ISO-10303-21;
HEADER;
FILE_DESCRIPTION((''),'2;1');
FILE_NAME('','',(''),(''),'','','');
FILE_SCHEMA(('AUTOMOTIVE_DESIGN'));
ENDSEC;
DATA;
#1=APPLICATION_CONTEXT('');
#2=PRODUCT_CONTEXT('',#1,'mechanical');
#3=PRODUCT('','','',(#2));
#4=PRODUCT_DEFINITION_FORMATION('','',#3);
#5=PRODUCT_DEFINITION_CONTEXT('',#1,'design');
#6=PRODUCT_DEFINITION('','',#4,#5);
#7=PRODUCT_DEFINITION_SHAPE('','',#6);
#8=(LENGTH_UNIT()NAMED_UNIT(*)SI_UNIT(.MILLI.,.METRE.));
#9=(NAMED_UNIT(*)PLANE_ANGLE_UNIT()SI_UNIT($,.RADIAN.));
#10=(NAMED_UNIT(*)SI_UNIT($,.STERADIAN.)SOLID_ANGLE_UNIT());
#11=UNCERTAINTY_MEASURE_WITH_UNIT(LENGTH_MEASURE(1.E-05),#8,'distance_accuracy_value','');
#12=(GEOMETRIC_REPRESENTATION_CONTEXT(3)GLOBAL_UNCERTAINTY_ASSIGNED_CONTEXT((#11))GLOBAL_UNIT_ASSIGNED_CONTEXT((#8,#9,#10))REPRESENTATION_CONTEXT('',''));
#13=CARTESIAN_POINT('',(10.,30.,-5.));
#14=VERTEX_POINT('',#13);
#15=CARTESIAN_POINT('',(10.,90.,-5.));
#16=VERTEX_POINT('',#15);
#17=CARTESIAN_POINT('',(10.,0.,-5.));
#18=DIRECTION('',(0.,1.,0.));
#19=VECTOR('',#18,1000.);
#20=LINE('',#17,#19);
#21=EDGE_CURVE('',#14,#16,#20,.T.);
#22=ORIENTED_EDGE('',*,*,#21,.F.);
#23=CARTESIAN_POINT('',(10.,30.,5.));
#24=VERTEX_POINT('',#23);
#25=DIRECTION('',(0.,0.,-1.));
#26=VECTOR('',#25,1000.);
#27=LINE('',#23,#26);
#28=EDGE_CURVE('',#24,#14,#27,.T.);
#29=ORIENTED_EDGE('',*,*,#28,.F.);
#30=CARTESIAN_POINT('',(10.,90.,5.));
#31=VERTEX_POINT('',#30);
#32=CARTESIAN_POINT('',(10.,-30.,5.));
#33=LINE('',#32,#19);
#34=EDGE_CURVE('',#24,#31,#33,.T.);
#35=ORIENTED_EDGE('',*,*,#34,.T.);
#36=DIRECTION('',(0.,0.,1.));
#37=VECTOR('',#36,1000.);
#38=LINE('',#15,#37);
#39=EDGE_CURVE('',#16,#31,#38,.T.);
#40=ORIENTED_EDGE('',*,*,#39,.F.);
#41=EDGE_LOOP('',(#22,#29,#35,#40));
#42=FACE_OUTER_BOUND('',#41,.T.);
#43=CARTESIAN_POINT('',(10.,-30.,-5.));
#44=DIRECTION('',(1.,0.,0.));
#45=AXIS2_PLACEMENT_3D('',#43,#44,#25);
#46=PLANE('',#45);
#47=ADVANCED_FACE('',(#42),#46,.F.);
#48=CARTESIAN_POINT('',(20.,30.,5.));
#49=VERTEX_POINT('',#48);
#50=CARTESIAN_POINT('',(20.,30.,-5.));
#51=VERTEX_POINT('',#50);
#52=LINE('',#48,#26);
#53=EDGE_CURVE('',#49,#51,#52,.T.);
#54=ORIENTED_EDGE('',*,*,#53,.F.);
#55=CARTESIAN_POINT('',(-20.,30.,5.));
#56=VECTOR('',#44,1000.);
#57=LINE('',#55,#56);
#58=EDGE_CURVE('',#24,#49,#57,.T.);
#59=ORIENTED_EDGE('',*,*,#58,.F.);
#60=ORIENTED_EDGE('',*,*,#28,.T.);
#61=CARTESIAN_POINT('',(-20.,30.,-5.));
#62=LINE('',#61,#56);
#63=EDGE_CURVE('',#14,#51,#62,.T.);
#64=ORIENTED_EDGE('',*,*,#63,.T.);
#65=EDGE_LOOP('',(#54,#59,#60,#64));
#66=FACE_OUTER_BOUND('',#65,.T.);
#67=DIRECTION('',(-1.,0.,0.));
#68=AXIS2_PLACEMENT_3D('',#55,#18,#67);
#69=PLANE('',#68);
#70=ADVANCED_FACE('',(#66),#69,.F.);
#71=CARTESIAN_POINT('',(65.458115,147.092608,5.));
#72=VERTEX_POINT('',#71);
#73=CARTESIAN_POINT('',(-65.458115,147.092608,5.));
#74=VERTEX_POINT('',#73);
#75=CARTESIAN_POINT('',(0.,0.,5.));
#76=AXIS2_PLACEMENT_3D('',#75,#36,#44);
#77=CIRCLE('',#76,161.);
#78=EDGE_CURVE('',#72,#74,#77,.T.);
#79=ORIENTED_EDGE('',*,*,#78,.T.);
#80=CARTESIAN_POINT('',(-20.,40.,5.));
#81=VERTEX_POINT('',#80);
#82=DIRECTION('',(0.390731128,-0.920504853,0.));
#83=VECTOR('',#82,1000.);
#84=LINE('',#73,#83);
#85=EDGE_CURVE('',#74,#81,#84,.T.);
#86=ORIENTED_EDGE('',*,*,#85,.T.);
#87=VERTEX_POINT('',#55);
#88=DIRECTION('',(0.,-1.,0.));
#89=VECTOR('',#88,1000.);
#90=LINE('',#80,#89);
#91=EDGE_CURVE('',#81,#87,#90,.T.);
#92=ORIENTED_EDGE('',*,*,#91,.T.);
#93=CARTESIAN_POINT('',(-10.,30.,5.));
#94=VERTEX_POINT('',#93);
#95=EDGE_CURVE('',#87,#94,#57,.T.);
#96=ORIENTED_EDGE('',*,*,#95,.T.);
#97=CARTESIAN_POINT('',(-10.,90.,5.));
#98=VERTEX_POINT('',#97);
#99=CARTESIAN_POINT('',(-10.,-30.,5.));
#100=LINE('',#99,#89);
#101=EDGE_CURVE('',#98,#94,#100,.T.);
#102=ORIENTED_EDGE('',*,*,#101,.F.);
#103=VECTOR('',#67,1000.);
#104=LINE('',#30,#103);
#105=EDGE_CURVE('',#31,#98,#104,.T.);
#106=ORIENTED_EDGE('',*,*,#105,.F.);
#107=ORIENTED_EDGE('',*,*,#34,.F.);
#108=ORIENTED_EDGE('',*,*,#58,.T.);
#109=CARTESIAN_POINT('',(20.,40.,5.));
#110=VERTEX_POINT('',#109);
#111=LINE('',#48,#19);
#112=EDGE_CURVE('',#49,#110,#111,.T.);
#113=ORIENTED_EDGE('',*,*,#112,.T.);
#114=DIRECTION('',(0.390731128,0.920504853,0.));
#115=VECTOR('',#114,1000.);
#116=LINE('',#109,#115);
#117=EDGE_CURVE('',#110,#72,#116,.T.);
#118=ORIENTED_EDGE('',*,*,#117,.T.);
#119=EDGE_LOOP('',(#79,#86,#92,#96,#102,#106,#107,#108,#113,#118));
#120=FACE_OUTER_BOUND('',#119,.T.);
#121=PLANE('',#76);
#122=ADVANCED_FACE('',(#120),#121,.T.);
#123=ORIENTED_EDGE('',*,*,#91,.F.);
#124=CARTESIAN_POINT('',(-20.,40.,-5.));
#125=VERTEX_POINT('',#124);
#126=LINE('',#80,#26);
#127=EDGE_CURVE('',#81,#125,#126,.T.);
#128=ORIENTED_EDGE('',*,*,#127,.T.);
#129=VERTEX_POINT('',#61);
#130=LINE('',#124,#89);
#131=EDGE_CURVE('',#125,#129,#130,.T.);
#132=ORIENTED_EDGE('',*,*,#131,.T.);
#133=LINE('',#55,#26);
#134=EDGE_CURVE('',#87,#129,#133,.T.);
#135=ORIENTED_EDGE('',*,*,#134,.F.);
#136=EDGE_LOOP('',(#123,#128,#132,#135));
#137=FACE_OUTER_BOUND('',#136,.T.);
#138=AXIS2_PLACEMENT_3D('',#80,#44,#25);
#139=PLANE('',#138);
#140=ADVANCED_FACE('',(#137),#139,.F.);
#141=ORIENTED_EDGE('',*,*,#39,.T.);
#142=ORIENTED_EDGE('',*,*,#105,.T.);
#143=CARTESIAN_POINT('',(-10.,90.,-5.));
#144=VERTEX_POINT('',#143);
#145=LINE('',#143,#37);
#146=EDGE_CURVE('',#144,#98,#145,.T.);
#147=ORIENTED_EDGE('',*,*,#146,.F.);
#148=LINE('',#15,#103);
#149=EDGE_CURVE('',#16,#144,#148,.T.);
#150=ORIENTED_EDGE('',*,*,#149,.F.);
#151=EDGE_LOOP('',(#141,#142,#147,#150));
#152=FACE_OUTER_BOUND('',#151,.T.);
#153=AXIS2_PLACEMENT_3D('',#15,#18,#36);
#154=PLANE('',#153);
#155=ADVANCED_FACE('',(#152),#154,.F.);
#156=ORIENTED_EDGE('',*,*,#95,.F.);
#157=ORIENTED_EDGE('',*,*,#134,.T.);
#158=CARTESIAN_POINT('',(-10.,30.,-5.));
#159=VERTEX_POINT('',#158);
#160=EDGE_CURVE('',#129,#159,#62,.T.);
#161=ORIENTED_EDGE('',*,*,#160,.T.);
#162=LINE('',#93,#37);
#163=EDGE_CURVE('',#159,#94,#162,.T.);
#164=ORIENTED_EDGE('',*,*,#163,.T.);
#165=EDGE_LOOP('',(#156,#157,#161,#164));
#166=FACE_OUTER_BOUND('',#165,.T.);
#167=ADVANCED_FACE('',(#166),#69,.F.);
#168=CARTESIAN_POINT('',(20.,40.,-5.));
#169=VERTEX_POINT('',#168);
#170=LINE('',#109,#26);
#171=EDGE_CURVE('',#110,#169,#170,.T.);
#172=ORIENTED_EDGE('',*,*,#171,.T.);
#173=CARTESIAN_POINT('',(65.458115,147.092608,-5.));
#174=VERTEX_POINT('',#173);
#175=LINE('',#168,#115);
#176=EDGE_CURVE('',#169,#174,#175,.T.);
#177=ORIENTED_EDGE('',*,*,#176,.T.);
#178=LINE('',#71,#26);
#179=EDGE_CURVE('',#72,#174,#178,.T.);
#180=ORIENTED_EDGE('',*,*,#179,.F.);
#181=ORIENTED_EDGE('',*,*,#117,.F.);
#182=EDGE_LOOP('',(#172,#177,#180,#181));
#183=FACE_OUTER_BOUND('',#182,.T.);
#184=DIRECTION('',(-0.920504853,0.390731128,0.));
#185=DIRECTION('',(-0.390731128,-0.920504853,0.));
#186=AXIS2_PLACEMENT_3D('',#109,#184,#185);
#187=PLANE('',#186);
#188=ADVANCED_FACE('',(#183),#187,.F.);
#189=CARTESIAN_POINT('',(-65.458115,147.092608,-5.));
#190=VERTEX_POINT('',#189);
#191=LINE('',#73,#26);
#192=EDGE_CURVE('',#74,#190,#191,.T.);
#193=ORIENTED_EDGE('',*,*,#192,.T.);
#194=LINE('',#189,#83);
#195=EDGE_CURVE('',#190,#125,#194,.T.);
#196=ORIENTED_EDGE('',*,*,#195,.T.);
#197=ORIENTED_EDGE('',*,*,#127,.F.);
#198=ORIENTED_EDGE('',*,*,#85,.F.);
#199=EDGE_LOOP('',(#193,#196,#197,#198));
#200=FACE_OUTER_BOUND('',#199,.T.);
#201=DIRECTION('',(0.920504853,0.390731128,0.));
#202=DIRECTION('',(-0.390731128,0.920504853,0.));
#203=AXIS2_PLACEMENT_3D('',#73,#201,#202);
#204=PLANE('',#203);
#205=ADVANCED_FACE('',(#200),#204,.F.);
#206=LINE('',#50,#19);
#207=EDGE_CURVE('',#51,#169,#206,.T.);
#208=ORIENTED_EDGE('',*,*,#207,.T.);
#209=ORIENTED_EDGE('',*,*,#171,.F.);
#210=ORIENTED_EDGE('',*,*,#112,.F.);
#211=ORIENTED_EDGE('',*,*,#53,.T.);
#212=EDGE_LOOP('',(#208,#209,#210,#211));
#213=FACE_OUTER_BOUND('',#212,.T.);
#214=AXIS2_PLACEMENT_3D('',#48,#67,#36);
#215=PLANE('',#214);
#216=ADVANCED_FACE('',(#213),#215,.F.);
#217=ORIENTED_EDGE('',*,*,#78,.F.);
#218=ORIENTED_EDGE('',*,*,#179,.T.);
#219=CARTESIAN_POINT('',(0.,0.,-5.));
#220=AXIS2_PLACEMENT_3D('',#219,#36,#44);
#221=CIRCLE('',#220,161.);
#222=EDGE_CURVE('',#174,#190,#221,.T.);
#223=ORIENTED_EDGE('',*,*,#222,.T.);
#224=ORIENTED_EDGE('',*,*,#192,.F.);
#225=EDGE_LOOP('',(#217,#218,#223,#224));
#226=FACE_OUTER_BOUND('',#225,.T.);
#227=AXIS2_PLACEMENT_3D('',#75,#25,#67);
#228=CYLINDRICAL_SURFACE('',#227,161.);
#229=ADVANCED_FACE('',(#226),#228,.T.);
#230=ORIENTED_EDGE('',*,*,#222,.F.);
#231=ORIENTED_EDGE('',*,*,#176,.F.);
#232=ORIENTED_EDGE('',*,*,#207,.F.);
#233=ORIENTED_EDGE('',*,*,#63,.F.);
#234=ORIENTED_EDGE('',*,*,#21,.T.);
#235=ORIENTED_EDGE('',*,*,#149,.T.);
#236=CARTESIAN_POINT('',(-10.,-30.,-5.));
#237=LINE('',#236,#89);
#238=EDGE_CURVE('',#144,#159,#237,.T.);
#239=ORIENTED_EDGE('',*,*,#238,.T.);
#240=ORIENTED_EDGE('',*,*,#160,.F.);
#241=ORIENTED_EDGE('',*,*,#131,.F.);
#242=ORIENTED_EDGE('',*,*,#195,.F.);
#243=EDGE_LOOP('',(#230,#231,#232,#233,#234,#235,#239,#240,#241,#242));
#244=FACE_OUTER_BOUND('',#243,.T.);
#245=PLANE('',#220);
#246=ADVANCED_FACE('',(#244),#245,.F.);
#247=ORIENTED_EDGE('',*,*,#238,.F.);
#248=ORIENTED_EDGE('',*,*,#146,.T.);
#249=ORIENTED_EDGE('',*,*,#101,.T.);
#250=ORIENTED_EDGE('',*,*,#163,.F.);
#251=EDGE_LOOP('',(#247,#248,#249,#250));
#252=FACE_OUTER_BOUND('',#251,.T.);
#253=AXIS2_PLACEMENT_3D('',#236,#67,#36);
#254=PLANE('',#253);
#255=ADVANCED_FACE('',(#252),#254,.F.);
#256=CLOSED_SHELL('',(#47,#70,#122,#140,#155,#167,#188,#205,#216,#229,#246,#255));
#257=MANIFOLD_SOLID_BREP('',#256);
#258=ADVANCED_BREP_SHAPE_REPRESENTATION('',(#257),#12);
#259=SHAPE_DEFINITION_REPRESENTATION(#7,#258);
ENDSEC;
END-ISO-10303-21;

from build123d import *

# Parameters (mm, degrees)
BOSS_EXTRUDE1_DEPTH = 5
SKETCH2_W           = 20
SKETCH2_H           = 120
CUT_EXTRUDE1_DEPTH  = 10


with BuildPart() as part:
    # Sketch1 → Boss-Extrude1 (new, symmetric)
    with BuildSketch(Plane.XY):
        with BuildLine():
            Line((-65.458114903, 147.092607541), (-20, 40))
            Line((-20, 40), (-20, 30))
            Line((-20, 30), (20, 30))
            Line((20, 30), (20, 40))
            Line((20, 40), (65.458114903, 147.092607541))
            ThreePointArc((65.458114903, 147.092607541), (0, 161), (-65.458114903, 147.092607541))
        make_face()
    extrude(amount=BOSS_EXTRUDE1_DEPTH, both=True)

    # Sketch2 → Cut-Extrude1 (cut)
    with BuildSketch(Plane.XY.offset(5)):
        with Locations((0, 30)):
            Rectangle(SKETCH2_W, SKETCH2_H)
    extrude(amount=-CUT_EXTRUDE1_DEPTH, mode=Mode.SUBTRACT)


solid = part.part
